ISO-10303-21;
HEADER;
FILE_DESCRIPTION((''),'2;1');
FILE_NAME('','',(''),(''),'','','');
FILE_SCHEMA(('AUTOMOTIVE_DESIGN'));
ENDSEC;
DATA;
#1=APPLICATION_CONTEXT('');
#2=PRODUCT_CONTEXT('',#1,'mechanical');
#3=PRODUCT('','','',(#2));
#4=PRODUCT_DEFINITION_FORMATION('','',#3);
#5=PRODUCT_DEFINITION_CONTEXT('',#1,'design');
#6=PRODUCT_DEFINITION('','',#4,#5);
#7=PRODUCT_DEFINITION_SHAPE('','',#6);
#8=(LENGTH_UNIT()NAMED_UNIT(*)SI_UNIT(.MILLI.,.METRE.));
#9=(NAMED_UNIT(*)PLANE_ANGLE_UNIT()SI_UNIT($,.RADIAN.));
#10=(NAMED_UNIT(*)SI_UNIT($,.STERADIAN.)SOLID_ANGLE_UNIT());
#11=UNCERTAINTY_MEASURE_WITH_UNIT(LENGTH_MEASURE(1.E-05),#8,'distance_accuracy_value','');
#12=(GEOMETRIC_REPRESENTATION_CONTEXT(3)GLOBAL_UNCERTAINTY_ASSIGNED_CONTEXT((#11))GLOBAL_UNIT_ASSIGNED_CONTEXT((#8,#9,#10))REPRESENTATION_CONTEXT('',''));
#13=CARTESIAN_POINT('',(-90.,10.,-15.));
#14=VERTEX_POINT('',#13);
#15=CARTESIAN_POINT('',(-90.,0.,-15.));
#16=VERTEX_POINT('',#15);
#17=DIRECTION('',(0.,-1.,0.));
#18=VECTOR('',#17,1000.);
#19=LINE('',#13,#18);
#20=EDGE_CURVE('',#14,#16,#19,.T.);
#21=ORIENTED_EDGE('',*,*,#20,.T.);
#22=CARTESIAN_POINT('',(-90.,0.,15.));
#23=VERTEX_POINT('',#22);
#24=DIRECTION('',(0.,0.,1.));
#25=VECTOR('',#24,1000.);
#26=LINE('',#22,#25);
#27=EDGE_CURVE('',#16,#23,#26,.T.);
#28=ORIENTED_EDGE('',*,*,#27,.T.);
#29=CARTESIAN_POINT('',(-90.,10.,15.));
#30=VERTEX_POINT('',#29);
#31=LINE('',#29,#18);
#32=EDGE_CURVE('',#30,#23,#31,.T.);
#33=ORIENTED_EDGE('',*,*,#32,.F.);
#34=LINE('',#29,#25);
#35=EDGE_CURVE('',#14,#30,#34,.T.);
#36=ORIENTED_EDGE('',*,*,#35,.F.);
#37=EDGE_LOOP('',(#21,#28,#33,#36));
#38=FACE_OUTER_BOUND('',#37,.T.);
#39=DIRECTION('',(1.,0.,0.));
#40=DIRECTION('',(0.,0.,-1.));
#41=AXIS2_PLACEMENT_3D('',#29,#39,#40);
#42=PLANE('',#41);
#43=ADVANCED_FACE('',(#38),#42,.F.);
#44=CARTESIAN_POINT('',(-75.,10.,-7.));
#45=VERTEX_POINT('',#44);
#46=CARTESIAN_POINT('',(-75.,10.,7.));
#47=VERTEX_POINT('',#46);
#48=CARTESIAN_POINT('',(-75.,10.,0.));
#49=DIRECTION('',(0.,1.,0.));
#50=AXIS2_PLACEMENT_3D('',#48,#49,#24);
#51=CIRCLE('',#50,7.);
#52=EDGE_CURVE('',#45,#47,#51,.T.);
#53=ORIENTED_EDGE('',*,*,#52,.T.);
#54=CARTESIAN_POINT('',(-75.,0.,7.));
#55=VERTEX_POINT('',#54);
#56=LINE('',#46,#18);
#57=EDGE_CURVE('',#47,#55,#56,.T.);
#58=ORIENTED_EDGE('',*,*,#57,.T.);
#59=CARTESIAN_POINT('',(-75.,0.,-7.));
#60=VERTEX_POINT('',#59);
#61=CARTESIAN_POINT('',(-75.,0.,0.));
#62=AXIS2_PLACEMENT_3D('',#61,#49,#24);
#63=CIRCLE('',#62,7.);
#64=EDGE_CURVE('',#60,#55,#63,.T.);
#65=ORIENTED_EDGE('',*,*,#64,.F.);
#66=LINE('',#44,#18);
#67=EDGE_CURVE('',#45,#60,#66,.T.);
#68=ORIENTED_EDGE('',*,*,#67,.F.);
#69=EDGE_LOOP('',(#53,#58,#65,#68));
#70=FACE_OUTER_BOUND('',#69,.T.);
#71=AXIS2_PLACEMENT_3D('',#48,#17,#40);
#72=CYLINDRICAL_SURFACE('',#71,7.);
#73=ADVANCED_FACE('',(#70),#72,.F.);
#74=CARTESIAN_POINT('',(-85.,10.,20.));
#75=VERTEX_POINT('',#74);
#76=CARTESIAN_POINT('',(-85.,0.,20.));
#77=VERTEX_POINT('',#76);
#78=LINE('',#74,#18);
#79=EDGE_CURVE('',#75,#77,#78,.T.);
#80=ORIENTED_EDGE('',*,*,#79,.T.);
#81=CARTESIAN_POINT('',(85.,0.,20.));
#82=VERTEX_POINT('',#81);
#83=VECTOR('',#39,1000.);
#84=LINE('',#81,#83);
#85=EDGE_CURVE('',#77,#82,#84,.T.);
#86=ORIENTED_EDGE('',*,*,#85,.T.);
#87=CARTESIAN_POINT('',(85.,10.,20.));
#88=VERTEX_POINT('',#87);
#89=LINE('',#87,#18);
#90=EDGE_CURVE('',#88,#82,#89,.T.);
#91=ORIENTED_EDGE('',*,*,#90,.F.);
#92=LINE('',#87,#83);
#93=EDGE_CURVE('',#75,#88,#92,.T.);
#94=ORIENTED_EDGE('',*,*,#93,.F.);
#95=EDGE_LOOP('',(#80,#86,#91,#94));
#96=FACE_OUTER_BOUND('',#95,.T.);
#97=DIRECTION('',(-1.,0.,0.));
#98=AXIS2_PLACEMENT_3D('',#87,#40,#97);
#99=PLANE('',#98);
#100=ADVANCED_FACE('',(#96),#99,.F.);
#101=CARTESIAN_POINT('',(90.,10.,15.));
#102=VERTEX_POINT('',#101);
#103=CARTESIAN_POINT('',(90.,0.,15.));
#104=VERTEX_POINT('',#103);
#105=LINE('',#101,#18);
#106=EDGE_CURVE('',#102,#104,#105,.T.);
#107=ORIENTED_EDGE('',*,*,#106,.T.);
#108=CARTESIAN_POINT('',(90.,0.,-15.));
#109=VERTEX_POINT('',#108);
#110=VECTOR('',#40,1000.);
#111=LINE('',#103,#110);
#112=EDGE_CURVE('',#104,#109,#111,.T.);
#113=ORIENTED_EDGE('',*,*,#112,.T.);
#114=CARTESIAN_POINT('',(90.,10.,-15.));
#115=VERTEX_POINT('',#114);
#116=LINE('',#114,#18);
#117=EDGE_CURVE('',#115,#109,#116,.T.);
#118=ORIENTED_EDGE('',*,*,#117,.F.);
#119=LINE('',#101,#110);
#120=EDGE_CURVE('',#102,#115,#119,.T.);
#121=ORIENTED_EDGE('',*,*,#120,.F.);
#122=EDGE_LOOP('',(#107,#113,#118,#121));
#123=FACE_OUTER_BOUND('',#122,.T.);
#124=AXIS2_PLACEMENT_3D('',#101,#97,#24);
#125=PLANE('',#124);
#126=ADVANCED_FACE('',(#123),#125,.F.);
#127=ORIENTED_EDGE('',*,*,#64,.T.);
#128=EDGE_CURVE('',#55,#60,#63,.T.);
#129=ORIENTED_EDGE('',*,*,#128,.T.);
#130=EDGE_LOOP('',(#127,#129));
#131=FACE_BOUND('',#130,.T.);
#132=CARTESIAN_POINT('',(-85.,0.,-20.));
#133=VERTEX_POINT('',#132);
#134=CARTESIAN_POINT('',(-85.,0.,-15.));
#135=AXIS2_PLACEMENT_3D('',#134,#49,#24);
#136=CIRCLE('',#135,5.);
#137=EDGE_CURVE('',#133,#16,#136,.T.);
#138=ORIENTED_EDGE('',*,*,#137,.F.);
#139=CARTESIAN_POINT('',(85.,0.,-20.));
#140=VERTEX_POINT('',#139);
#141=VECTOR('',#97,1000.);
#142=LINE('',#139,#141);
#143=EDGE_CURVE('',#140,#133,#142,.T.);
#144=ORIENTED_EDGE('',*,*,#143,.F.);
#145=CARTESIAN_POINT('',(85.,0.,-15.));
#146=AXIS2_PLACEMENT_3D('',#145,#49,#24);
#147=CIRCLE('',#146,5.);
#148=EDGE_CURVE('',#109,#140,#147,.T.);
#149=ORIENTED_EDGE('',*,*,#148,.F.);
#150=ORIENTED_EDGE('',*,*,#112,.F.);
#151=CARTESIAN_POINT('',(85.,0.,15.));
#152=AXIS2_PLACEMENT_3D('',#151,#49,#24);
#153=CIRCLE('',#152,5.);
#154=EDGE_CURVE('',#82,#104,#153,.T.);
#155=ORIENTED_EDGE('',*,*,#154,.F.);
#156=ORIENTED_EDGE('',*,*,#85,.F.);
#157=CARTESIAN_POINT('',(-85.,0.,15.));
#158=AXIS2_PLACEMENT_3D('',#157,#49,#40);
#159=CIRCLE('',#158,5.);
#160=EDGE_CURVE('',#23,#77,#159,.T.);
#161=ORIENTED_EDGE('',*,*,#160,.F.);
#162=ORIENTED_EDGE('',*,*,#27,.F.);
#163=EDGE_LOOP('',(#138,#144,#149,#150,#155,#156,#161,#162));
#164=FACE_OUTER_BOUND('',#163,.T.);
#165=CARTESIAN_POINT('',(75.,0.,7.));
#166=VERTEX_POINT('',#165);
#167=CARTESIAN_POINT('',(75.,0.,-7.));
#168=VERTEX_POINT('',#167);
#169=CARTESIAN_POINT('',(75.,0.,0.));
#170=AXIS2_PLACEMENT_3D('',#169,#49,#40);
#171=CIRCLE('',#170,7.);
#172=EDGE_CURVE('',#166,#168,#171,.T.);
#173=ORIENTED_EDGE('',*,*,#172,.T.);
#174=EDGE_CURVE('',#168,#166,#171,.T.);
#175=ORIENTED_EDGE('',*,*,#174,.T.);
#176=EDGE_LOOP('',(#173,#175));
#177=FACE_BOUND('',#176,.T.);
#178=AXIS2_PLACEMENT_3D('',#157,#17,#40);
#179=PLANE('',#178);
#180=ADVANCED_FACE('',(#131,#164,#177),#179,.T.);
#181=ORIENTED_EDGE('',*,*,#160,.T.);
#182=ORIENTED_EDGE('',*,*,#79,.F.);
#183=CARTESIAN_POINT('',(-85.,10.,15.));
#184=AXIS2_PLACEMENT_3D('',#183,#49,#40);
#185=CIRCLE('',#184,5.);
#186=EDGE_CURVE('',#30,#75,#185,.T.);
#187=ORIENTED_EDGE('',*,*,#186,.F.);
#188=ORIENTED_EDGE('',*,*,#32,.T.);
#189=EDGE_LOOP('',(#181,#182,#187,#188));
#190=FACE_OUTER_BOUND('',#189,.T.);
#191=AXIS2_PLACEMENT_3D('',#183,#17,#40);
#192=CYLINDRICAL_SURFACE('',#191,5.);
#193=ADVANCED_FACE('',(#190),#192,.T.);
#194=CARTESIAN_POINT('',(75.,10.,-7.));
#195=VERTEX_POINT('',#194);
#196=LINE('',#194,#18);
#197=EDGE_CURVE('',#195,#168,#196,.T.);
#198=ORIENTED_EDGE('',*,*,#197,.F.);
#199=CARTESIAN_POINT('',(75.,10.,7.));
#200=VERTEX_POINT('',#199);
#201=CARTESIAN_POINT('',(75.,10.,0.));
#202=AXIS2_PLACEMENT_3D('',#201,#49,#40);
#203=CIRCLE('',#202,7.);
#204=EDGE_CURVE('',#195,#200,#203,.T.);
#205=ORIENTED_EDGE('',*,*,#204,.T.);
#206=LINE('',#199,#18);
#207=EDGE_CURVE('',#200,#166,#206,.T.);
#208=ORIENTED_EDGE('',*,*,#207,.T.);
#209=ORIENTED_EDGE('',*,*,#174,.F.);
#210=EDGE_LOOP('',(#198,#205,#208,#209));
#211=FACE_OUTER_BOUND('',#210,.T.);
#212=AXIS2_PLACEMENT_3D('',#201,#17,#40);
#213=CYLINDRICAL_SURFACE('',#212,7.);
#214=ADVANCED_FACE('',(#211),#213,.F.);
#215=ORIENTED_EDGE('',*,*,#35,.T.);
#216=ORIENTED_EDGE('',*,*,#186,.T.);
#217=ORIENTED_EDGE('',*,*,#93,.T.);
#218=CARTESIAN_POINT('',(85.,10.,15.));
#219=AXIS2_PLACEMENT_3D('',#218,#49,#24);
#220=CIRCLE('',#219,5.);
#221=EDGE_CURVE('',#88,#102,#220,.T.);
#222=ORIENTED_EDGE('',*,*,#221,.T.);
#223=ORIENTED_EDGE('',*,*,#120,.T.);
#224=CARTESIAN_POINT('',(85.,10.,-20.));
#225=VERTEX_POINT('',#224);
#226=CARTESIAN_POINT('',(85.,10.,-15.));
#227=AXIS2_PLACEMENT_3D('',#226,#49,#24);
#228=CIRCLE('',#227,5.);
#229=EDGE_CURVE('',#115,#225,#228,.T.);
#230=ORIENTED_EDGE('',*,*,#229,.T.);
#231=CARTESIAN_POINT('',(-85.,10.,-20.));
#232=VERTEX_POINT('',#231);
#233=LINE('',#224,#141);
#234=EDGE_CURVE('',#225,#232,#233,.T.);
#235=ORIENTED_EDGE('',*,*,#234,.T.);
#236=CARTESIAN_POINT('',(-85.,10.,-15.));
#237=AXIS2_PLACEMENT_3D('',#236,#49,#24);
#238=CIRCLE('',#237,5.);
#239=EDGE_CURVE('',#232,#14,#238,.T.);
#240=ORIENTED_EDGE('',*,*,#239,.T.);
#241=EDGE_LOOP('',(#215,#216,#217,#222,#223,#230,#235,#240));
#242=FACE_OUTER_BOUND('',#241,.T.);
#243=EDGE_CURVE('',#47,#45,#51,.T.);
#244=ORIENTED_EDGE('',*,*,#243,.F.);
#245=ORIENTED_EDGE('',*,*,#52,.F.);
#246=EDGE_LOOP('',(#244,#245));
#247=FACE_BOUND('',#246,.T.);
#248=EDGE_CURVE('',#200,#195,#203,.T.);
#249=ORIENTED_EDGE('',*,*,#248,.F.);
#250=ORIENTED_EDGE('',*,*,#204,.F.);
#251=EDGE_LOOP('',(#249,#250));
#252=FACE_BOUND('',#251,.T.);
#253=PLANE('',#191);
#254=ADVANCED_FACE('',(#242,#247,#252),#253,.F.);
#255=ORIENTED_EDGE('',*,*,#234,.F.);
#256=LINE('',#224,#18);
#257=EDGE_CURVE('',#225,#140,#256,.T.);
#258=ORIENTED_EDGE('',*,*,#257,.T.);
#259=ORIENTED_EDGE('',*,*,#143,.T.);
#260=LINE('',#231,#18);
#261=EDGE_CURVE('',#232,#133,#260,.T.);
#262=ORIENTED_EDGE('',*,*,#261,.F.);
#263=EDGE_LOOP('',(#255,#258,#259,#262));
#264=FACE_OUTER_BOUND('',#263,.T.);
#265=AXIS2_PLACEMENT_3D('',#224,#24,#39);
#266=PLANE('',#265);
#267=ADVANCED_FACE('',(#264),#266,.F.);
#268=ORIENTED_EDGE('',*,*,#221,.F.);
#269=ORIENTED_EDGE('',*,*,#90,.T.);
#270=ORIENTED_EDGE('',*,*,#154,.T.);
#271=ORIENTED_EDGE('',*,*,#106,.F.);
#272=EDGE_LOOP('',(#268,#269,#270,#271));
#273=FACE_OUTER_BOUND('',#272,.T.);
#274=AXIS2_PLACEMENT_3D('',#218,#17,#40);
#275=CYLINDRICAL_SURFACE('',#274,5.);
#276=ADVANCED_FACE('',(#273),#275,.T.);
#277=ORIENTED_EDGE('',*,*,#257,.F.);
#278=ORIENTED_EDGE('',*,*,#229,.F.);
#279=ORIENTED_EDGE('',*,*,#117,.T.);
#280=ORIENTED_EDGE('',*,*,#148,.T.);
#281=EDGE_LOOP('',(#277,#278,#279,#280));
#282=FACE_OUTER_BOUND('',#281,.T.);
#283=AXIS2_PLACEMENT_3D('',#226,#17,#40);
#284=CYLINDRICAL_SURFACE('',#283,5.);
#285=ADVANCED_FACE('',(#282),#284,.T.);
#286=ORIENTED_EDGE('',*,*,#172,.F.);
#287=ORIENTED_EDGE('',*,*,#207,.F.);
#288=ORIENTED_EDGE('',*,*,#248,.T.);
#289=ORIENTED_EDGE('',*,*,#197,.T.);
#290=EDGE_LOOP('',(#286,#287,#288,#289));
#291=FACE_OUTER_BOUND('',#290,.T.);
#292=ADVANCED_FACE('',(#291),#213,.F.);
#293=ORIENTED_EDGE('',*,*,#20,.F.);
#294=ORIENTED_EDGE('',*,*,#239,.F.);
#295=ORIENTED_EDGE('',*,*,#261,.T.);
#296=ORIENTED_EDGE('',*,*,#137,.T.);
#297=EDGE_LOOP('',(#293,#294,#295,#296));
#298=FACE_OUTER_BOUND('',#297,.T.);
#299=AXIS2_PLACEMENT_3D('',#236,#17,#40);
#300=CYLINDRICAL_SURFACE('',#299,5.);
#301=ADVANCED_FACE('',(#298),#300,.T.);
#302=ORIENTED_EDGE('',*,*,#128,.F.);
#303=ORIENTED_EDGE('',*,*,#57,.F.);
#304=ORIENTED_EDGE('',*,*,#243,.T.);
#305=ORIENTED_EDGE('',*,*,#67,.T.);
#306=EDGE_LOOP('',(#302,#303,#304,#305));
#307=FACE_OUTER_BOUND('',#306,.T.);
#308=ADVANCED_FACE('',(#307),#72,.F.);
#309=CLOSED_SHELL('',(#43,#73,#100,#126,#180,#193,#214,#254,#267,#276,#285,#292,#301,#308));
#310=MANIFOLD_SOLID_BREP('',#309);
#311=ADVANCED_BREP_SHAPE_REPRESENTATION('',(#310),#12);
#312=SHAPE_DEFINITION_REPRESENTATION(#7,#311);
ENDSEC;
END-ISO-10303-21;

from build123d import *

# Parameters (mm, degrees)
SKETCH2_R           = 7
BOSS_EXTRUDE1_DEPTH = 10


with BuildPart() as part:
    # Sketch2 → Boss-Extrude1 (new body)
    with BuildSketch(Plane(origin=(0, 0, 0), x_dir=(1, 0, 0), z_dir=(0, 1, 0))):
        with BuildLine():
            Line((85, -20), (-85, -20))
            ThreePointArc((-85, -20), (-88.535533906, -18.535533906), (-90, -15))
            Line((-90, -15), (-90, 15))
            ThreePointArc((-90, 15), (-88.535533906, 18.535533906), (-85, 20))
            Line((-85, 20), (85, 20))
            ThreePointArc((85, 20), (88.535533906, 18.535533906), (90, 15))
            Line((90, 15), (90, -15))
            ThreePointArc((90, -15), (88.535533906, -18.535533906), (85, -20))
        make_face()
        with Locations(Location((-75, 0, 0), (0, 0, 270))):
            Circle(SKETCH2_R, mode=Mode.SUBTRACT)
        with Locations(Location((75, 0, 0), (0, 0, 90))):
            Circle(SKETCH2_R, mode=Mode.SUBTRACT)
    extrude(amount=BOSS_EXTRUDE1_DEPTH)


solid = part.part
